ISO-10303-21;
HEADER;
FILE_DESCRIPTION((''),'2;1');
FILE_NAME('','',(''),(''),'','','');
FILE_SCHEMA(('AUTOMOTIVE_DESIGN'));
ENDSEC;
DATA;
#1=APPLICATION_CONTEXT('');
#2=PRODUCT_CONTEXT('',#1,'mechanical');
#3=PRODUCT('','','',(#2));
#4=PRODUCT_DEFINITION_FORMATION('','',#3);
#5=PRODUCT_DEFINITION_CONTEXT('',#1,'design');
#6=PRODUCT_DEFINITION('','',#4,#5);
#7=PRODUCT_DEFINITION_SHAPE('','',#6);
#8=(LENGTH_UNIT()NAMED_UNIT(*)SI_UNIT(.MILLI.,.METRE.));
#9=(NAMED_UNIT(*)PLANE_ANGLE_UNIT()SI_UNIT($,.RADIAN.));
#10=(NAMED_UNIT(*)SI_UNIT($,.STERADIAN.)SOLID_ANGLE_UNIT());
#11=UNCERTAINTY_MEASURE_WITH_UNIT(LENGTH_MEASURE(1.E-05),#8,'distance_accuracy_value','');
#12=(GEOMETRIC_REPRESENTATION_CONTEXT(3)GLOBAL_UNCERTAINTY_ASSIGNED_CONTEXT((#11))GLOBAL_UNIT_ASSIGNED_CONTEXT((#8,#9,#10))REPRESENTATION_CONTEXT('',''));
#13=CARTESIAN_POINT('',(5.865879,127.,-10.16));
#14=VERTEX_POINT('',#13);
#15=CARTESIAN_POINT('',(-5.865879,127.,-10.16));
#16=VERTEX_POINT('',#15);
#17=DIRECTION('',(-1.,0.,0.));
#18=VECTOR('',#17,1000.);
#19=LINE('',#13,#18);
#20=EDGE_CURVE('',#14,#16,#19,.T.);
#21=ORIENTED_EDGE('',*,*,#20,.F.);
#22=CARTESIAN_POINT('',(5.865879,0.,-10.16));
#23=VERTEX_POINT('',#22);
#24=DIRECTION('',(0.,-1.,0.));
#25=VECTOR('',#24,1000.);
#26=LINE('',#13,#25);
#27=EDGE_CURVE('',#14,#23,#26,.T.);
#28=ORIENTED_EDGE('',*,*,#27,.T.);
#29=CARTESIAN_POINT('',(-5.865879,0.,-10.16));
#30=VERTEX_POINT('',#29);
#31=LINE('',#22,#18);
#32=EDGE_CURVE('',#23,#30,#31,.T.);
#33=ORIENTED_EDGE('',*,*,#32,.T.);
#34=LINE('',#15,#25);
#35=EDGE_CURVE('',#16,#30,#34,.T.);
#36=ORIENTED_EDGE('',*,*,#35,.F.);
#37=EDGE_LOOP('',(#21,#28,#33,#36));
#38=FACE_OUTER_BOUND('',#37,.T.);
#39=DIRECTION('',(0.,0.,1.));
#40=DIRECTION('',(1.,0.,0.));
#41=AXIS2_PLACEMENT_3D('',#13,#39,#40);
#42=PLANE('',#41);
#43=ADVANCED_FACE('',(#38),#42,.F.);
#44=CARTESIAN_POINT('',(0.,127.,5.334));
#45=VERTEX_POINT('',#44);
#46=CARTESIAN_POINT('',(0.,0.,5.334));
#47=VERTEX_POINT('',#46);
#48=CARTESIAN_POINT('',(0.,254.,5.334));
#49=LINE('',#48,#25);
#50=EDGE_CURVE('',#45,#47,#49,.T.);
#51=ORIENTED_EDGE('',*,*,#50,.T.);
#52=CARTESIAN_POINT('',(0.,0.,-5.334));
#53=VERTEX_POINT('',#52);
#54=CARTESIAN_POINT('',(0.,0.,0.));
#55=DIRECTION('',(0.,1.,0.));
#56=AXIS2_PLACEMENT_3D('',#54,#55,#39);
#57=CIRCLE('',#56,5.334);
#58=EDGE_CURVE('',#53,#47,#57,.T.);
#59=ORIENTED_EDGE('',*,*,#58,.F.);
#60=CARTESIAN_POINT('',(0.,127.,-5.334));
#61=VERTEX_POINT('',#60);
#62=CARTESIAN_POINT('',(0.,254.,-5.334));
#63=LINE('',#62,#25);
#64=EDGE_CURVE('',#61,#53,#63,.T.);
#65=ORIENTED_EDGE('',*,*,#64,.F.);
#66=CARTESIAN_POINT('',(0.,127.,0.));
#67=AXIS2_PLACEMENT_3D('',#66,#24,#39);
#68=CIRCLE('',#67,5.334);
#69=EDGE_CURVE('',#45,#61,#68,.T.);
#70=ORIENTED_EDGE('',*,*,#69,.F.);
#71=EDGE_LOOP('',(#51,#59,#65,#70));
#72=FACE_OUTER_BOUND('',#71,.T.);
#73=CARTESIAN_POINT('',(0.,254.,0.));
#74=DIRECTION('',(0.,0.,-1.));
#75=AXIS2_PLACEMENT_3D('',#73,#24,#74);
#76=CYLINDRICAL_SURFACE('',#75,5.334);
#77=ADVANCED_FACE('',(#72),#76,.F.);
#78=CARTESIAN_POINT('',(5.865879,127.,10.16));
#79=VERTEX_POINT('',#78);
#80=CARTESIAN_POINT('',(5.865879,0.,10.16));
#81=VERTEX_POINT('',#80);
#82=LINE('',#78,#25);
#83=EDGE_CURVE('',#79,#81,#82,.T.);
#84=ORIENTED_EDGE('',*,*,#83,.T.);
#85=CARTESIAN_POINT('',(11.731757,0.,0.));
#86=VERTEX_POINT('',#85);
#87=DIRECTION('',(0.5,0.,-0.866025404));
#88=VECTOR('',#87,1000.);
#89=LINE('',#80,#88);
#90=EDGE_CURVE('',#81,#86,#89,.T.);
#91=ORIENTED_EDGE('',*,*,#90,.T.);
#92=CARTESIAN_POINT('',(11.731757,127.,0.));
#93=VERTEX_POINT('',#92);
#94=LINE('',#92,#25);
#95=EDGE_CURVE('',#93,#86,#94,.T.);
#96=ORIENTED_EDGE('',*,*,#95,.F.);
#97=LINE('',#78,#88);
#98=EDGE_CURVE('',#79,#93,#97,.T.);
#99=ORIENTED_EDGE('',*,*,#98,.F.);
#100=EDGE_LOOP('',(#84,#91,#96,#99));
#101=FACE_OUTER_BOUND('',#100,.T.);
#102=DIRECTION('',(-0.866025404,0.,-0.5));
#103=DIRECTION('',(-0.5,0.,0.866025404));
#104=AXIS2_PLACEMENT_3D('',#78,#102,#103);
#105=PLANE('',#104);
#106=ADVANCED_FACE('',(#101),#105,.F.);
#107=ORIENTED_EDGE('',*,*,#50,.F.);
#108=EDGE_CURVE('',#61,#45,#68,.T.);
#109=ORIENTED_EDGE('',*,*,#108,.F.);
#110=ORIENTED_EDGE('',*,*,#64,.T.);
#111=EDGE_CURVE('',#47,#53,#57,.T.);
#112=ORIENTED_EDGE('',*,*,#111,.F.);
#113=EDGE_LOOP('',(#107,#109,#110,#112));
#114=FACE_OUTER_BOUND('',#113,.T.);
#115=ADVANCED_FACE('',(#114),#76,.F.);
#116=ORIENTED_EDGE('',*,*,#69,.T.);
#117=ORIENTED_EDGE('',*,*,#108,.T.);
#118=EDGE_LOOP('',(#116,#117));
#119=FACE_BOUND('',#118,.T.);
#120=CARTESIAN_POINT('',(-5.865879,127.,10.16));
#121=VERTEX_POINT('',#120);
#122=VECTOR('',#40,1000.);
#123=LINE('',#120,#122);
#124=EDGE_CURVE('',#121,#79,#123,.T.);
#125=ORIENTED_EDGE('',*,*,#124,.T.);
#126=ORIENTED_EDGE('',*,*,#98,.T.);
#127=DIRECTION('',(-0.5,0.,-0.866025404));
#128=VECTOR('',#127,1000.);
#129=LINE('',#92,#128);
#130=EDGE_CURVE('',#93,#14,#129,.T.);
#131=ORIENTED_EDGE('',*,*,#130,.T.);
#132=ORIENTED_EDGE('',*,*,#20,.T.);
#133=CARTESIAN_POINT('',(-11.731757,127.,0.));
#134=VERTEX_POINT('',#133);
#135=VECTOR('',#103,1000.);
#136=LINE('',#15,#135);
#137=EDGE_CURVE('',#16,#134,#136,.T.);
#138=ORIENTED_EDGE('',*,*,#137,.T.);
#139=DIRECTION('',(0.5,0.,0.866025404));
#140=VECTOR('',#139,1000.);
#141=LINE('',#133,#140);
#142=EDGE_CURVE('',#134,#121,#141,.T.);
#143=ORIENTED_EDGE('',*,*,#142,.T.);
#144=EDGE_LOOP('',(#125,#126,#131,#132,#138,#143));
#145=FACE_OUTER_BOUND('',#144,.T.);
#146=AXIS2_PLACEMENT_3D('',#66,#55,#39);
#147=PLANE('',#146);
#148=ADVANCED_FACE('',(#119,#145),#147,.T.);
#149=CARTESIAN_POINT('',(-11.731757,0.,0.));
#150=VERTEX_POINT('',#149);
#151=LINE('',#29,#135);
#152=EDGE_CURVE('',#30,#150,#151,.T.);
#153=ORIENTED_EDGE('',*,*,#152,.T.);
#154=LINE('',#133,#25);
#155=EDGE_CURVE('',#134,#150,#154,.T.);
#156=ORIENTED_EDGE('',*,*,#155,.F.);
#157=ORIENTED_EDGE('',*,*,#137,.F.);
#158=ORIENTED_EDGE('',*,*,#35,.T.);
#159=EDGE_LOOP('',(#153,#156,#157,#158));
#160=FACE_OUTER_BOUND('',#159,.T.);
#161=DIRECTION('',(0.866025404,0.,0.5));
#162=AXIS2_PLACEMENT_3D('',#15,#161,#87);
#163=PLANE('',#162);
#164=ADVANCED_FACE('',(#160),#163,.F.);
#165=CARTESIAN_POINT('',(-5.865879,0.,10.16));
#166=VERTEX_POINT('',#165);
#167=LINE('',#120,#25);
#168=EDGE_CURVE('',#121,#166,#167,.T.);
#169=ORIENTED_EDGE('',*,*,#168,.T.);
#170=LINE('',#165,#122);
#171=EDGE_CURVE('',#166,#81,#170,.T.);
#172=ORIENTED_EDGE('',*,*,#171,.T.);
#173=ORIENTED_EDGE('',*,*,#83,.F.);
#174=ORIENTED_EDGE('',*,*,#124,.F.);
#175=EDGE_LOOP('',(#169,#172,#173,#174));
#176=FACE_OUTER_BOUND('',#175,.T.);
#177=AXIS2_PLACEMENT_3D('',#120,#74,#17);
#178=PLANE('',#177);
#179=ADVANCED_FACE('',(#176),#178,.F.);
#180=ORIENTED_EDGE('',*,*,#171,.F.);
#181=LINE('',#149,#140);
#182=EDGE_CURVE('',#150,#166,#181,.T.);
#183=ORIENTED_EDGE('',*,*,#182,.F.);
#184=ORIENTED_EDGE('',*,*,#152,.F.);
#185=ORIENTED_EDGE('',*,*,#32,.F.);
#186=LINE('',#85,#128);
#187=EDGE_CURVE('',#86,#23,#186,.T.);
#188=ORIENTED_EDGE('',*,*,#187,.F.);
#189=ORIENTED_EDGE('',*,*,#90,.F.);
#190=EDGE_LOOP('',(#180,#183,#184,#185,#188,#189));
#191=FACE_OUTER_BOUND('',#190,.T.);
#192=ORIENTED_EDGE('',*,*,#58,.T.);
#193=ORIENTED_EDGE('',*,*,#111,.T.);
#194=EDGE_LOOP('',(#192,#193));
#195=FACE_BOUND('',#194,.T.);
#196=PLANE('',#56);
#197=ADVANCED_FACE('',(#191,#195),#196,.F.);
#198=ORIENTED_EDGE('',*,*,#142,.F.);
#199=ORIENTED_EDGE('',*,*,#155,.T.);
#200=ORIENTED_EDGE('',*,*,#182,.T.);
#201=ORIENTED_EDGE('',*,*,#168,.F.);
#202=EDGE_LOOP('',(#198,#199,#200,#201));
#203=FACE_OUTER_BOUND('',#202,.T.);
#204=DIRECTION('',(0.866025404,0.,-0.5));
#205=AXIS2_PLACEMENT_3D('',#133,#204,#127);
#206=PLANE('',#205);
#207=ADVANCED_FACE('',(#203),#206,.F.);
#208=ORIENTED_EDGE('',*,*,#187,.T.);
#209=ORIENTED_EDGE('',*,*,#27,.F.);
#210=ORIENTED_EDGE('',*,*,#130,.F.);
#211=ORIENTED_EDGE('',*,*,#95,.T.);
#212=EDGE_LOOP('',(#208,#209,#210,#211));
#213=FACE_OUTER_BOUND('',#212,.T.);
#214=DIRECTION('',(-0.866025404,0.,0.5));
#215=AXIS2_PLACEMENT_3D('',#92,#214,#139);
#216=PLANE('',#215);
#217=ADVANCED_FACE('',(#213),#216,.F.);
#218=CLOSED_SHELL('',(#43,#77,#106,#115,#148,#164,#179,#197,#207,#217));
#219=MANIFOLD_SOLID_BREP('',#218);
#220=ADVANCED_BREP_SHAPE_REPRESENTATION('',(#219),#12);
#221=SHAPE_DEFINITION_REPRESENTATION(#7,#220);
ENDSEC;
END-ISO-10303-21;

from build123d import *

# Parameters (mm, degrees)
BOSS_EXTRUDE1_DEPTH = 63.5
SKETCH2_R           = 2.667
CUT_EXTRUDE1_DEPTH  = 127
SCALE1_SCALE        = 2


with BuildPart() as part:
    # Sketch1 → Boss-Extrude1 (new body)
    with BuildSketch(Plane(origin=(0, 0, 0), x_dir=(1, 0, 0), z_dir=(0, 1, 0))):
        Polygon((2.932939367, -5.08), (5.865878735, 0), (2.932939367, 5.08), (-2.932939367, 5.08), (-5.865878735, 0), (-2.932939367, -5.08), align=None)
    extrude(amount=BOSS_EXTRUDE1_DEPTH)

    # Sketch2 → Cut-Extrude1 (cut)
    with BuildSketch(Plane(origin=(0, 0, 0), x_dir=(1, 0, 0), z_dir=(0, 1, 0))):
        with Locations(Location((0, 0, 0), (0, 0, 270))):
            Circle(SKETCH2_R)
    extrude(amount=CUT_EXTRUDE1_DEPTH, mode=Mode.SUBTRACT)


with BuildPart() as part_1:
    # Scale1: scaled about (0, 0, 0)
    add(part.part.scale(SCALE1_SCALE))


solid = part_1.part
